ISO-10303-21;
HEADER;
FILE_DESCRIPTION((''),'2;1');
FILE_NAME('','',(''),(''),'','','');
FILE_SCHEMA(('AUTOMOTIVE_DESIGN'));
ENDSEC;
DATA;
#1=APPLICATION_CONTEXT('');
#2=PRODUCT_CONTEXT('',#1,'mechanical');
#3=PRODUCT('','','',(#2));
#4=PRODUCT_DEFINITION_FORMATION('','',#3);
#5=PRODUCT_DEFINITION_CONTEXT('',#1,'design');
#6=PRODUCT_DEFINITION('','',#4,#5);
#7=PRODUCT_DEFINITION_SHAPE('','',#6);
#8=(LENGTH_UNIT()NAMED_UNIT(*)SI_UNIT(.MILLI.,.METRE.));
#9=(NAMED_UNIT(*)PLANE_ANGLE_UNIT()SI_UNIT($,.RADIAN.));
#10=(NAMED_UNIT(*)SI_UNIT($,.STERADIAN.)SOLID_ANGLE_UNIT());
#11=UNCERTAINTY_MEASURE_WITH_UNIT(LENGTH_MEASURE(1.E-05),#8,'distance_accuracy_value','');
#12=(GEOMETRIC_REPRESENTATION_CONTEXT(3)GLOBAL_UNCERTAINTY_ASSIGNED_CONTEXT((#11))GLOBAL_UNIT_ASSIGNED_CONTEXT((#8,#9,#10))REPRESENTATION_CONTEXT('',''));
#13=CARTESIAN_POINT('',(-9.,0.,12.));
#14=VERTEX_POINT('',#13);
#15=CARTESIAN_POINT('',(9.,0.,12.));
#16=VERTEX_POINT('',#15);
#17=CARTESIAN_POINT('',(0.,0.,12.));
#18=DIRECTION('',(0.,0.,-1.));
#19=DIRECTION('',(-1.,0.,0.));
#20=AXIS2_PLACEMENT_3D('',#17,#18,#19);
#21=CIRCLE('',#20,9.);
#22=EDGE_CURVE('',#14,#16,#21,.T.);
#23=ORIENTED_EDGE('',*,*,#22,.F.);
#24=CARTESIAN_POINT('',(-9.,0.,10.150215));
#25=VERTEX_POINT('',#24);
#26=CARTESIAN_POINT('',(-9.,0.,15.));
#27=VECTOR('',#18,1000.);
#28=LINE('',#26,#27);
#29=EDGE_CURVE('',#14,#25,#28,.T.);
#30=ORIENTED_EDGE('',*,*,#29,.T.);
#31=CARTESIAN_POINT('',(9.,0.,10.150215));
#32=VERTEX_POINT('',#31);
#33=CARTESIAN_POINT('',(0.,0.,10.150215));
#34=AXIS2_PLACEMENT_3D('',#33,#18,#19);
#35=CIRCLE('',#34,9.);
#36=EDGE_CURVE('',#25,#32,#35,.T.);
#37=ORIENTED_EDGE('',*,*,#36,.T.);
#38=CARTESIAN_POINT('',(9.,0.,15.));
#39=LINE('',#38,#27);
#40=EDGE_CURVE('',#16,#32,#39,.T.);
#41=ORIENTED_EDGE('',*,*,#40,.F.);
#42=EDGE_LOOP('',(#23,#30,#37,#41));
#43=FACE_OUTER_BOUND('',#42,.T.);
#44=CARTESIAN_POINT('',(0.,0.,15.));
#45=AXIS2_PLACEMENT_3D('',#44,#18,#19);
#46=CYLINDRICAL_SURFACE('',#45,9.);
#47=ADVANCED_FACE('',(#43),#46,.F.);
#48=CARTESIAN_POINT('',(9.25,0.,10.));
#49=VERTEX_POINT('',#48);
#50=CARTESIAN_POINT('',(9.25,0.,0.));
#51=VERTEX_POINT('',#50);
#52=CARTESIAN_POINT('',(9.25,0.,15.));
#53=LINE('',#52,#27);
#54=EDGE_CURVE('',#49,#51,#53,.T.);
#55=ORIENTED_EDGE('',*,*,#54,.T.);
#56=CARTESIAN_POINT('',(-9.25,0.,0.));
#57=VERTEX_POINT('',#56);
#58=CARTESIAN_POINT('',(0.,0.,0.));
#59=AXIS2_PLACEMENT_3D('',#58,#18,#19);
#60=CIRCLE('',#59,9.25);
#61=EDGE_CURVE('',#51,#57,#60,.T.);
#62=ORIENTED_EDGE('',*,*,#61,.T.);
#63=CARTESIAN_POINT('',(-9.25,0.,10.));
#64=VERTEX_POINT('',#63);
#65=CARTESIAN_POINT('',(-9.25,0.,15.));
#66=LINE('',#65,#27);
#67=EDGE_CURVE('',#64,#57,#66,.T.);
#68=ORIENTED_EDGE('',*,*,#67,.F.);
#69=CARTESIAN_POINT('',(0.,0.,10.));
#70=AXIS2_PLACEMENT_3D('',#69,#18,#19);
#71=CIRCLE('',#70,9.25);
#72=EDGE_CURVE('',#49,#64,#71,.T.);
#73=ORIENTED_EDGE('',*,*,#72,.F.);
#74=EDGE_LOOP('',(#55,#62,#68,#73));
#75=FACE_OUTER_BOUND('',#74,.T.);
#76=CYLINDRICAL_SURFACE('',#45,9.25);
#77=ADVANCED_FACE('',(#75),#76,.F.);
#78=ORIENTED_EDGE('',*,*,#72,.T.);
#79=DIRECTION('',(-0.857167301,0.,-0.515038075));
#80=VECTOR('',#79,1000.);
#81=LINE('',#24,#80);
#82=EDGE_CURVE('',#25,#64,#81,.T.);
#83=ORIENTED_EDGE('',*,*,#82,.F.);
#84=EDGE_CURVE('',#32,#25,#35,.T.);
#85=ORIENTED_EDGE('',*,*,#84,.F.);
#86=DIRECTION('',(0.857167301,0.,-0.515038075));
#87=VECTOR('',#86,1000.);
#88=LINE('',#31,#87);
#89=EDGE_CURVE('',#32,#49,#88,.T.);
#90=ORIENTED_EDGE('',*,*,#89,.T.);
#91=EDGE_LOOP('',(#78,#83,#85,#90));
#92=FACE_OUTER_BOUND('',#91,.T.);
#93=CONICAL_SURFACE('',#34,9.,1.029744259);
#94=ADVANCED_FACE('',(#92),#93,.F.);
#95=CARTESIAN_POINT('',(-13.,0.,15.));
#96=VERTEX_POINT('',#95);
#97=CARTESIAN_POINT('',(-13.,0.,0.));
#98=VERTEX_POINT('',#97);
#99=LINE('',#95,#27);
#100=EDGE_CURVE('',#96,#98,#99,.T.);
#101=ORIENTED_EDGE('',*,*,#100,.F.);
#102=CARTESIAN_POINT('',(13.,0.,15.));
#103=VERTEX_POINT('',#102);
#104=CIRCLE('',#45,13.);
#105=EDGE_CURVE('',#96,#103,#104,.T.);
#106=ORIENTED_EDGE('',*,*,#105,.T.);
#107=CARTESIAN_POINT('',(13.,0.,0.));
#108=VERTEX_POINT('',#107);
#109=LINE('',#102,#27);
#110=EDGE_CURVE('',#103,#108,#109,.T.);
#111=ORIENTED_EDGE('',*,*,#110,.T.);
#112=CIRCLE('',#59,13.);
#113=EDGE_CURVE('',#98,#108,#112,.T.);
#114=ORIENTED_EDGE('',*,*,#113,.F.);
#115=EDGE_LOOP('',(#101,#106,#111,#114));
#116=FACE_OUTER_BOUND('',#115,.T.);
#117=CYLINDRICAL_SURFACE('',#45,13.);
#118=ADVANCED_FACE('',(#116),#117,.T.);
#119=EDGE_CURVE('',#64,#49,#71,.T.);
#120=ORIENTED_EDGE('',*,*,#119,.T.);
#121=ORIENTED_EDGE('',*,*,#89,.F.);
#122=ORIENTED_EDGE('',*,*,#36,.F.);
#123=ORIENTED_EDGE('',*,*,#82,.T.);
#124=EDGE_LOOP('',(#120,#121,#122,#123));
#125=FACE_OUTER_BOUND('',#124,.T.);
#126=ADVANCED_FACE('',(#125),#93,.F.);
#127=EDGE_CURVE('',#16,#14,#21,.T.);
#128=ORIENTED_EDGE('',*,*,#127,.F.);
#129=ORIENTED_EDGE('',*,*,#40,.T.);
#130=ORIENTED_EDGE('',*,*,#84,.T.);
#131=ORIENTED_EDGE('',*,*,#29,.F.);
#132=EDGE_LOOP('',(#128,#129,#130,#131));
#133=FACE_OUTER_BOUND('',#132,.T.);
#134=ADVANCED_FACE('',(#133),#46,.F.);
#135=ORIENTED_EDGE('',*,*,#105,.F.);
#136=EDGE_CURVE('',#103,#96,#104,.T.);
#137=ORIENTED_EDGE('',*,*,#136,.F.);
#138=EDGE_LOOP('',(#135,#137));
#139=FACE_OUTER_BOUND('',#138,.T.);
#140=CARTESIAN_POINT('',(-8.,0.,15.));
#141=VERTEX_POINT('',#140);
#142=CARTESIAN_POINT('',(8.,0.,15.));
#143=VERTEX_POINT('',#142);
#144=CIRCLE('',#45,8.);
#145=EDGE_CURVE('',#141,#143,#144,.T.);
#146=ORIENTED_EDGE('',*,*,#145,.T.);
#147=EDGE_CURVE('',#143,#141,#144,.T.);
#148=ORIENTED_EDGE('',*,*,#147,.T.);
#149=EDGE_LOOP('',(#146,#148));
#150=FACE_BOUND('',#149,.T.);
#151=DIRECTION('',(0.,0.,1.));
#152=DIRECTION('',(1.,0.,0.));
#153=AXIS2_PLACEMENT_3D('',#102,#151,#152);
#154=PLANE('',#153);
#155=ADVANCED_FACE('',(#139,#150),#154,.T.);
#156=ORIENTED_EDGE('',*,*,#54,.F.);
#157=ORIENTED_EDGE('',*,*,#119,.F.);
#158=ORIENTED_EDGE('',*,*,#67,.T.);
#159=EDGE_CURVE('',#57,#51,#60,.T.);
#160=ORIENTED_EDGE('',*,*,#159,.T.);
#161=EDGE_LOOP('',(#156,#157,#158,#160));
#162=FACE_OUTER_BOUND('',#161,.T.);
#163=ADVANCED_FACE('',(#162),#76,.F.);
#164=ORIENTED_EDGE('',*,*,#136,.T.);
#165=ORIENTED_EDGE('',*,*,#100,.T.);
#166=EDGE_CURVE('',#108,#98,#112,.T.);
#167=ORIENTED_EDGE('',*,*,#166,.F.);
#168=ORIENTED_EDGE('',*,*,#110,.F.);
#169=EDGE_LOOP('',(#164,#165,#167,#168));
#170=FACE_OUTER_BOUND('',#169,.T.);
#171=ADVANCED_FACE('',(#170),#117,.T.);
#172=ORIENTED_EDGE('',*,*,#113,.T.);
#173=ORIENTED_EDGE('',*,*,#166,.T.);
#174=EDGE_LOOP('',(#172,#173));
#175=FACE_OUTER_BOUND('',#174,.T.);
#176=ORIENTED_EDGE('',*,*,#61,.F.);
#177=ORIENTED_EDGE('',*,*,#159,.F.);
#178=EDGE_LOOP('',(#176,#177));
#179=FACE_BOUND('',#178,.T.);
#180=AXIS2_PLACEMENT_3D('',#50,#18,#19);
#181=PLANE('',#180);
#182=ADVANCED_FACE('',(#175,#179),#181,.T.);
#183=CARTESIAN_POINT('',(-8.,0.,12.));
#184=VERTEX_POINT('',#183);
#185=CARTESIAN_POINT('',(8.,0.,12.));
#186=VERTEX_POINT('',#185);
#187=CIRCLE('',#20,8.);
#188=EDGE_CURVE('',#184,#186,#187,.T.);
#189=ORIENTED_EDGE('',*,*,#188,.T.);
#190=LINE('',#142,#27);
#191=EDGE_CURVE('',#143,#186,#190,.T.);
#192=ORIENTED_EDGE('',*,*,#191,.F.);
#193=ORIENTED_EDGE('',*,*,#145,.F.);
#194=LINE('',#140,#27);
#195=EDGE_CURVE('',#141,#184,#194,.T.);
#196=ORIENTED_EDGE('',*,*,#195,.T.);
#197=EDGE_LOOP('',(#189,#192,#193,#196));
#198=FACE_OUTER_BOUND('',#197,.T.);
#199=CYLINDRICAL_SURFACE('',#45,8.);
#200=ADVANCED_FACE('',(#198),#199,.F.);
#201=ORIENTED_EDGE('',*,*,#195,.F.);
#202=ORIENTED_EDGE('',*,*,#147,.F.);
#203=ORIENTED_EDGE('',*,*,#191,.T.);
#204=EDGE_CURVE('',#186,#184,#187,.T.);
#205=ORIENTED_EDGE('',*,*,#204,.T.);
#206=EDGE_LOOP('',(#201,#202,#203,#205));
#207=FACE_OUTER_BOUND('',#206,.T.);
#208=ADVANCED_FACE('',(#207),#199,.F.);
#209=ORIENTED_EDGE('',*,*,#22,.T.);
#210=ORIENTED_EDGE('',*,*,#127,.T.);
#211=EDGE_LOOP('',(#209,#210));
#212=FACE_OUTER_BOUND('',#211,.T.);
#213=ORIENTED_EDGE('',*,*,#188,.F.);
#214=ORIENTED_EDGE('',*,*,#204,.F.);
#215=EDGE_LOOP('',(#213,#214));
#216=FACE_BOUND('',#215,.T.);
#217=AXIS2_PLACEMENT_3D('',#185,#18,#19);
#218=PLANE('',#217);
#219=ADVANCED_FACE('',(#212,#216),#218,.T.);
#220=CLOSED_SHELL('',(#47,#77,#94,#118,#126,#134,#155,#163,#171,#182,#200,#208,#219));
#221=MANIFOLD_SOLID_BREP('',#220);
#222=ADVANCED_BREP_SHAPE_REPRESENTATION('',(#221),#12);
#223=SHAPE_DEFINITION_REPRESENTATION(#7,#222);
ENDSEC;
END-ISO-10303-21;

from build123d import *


with BuildPart() as part:
    # Sketch1 → Revolve1 (revolve)
    with BuildSketch(Plane.XZ, mode=Mode.PRIVATE) as revolve1_sk:
        Polygon((9.25, 0), (13, 0), (13, 15), (8, 15), (8, 12), (9, 12), (9, 10.150215155), (9.25, 10), align=None)
    revolve(revolve1_sk.sketch.rotate(Axis((0, 0, 15), (0, 0, -1)), 180), axis=Axis((0, 0, 15), (0, 0, -1)))


solid = part.part
